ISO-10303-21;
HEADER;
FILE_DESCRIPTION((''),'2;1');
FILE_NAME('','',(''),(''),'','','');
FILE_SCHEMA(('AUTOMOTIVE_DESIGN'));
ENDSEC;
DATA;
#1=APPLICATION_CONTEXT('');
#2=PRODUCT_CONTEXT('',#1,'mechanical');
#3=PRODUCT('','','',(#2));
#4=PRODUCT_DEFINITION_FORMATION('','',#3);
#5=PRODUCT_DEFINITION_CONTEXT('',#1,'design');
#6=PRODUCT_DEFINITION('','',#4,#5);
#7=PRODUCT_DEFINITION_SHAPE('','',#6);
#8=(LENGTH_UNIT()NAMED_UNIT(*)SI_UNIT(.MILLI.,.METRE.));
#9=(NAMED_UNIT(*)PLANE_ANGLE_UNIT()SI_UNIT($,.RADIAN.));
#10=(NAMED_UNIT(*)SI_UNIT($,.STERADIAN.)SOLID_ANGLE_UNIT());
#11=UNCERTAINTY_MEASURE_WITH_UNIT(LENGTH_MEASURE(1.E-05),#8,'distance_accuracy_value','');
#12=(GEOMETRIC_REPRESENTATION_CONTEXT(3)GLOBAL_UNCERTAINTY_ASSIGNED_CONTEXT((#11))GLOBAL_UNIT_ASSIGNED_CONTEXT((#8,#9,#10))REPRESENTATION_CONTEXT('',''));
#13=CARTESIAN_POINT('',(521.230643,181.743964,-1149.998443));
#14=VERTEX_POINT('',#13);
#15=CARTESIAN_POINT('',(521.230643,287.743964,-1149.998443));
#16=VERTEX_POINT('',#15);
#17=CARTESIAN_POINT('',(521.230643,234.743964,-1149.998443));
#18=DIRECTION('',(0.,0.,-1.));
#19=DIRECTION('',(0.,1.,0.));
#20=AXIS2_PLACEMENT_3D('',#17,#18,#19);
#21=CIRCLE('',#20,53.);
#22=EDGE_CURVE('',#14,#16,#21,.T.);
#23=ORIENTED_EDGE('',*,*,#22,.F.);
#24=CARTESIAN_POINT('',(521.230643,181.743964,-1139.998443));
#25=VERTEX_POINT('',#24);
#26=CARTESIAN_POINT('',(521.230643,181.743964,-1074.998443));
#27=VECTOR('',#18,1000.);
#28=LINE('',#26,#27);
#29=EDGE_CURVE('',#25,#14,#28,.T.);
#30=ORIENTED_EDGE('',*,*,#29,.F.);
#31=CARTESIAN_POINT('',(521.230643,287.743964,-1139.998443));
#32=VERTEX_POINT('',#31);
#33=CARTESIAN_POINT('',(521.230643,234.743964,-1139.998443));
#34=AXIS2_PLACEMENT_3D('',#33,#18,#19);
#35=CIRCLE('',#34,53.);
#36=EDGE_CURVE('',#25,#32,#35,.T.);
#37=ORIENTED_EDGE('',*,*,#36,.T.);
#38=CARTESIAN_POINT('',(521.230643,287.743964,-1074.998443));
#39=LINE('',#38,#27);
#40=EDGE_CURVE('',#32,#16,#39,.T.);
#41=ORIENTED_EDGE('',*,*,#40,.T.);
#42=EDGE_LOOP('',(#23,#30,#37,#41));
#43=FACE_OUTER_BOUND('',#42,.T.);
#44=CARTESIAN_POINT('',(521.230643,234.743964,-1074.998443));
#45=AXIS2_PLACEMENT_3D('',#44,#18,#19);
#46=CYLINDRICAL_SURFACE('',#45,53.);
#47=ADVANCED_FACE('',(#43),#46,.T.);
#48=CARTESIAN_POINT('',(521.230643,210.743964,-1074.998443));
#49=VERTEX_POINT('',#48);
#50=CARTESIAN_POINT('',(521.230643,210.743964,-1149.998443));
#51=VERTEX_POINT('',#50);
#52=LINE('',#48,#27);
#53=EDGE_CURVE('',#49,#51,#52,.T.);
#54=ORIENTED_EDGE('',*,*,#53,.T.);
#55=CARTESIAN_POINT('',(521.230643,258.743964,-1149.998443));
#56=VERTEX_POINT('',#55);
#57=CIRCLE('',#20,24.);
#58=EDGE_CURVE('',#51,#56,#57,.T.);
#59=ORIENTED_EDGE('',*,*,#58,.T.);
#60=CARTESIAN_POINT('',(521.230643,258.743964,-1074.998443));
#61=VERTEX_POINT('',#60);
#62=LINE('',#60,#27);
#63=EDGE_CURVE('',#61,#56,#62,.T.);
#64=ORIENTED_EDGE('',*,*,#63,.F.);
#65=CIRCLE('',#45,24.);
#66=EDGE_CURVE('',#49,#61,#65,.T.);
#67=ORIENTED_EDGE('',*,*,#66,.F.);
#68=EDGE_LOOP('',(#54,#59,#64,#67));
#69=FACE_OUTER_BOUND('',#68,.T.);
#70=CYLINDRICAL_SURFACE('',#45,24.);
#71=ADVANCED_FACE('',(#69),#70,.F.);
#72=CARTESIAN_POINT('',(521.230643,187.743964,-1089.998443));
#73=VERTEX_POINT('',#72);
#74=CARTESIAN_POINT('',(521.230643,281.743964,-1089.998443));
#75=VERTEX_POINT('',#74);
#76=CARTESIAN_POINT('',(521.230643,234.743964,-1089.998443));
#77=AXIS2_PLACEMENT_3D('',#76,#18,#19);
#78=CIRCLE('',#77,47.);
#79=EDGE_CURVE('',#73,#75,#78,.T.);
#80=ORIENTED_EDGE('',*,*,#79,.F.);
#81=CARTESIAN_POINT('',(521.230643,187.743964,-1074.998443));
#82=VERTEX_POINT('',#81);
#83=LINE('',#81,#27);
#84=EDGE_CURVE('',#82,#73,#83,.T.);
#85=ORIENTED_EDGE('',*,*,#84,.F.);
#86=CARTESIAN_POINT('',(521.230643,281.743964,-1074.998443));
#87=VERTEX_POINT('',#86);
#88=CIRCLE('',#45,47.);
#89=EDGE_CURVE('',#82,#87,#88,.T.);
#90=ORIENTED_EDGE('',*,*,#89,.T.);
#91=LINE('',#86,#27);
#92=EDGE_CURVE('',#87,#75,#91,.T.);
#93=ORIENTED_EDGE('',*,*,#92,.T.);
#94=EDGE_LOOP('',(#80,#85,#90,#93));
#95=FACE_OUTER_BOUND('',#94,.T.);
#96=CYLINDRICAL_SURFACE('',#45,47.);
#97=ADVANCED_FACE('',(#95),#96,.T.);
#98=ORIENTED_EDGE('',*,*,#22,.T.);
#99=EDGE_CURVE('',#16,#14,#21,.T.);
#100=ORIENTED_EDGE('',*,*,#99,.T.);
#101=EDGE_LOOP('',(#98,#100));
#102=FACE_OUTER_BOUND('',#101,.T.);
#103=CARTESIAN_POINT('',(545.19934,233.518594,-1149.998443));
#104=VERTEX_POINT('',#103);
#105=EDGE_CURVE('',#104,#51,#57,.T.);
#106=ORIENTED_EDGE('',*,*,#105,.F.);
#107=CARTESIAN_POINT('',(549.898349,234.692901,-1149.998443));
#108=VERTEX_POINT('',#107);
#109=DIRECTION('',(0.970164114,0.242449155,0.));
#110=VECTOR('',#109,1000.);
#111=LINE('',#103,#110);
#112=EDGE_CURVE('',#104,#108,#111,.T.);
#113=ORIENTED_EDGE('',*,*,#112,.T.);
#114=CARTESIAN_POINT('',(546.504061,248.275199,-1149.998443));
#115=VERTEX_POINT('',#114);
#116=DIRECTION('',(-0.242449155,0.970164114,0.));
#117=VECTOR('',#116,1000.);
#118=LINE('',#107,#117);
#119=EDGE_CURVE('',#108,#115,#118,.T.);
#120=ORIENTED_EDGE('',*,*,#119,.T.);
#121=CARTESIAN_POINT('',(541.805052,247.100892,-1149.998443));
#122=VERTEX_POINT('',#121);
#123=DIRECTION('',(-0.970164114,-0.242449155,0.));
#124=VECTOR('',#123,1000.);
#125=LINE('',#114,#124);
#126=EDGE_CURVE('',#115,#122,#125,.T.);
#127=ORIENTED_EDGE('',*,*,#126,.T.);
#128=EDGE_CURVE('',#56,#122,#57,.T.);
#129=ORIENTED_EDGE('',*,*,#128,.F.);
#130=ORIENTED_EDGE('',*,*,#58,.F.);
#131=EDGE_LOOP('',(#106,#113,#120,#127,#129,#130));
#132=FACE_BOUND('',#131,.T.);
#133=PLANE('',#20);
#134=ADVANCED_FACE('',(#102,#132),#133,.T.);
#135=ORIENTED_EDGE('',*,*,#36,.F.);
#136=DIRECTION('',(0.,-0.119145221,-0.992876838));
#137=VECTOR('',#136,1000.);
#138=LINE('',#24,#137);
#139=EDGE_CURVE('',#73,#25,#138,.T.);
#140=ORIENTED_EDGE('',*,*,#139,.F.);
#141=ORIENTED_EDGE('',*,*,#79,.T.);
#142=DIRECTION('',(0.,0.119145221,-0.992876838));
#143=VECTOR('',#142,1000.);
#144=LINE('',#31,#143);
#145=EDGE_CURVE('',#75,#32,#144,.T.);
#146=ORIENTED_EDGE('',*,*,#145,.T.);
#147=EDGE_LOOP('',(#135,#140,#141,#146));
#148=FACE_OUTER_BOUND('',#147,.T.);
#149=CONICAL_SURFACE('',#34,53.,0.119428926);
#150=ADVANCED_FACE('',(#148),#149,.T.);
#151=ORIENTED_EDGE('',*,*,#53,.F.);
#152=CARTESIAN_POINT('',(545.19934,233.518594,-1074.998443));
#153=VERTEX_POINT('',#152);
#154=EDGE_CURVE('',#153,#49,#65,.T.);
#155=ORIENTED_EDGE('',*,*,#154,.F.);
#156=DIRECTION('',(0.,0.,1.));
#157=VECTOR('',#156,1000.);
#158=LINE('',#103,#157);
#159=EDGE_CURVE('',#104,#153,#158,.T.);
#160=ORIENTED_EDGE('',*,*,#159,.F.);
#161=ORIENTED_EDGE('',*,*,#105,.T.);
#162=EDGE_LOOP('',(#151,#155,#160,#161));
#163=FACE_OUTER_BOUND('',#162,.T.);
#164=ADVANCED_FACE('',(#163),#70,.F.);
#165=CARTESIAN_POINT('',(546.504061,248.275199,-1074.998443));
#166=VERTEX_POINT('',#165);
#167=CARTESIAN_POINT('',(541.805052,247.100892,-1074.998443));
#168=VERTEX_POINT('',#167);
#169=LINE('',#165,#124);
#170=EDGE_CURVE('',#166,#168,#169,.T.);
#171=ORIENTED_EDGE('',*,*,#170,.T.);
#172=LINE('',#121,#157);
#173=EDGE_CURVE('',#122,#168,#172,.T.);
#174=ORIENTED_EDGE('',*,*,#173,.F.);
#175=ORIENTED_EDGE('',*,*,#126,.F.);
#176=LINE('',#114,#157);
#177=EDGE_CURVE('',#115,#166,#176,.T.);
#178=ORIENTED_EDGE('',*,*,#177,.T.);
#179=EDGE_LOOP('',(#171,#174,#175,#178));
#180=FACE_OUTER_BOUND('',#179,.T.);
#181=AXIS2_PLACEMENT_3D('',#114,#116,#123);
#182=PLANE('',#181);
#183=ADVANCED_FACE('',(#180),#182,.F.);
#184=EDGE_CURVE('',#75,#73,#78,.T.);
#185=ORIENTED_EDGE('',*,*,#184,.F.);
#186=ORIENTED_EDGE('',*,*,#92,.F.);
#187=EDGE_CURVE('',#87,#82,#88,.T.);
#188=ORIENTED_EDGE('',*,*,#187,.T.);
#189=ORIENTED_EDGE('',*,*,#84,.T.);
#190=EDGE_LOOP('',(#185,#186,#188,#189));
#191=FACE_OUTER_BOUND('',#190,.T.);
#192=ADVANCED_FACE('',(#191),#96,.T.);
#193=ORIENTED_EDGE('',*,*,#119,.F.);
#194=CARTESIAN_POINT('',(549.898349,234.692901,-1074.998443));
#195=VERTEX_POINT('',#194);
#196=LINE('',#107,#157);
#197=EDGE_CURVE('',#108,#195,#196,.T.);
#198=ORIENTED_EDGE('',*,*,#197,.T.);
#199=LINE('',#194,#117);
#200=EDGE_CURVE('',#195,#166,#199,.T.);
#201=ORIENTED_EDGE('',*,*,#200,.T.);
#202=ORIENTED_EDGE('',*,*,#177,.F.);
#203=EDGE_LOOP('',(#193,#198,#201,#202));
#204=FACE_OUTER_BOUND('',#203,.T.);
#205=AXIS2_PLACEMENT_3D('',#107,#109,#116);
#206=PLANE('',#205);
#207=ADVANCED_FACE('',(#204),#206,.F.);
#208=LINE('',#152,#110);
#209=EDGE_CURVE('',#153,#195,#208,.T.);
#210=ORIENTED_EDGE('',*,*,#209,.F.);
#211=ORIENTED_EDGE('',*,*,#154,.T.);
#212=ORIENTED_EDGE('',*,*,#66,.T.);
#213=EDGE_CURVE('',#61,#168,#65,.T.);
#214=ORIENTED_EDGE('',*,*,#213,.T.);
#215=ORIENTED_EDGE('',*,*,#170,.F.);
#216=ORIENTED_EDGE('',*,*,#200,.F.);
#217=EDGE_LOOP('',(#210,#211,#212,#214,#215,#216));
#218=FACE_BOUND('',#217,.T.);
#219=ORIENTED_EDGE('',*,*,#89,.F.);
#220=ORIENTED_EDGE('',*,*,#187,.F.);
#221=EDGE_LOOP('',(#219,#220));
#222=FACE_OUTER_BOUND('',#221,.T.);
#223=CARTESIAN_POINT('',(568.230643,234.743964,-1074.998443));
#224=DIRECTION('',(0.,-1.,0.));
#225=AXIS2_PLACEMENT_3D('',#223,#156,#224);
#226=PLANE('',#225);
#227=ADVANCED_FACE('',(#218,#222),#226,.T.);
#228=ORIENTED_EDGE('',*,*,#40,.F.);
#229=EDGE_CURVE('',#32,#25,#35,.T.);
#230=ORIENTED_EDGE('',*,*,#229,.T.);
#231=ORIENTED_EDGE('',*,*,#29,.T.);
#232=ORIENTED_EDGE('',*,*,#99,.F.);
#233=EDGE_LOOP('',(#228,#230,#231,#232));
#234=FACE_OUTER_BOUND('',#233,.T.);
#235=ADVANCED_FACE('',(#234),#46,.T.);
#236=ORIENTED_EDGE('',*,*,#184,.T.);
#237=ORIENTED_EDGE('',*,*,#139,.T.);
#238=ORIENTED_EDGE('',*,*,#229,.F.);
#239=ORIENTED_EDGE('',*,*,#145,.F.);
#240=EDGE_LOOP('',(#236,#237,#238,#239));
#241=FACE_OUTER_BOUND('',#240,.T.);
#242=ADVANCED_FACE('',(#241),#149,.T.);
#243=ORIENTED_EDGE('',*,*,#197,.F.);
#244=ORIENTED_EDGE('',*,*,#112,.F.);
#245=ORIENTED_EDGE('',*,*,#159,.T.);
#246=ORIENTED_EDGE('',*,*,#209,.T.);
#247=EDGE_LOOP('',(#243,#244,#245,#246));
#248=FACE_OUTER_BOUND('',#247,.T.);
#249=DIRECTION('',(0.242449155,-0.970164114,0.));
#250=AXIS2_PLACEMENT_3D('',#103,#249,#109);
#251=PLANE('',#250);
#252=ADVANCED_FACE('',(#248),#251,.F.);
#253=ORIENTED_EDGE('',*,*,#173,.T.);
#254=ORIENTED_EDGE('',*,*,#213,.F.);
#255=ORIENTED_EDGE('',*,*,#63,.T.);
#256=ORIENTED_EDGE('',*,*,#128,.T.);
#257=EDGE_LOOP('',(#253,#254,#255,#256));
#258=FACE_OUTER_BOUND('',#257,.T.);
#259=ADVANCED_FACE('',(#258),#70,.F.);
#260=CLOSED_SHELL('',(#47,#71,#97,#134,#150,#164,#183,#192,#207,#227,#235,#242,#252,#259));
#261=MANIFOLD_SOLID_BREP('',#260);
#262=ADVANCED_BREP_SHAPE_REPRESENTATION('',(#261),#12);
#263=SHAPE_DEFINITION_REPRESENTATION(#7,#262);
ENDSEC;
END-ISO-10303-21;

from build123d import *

# Parameters (mm, degrees)
CUT_EXTRUDE1_DEPTH = 647.654791602
SKETCH3_W          = 24
SKETCH3_H          = 75


with BuildPart() as part:
    # Sketch1 → Revolve1 (revolve)
    with BuildSketch(Plane.XZ.offset(-234.743963655), mode=Mode.PRIVATE) as revolve1_sk:
        Polygon((568.230642584, -1074.998443067), (521.230642584, -1074.998443067), (521.230642584, -1149.998443067), (574.230642584, -1149.998443067), (574.230642584, -1139.998443067), (568.230642584, -1089.998443067), align=None)
    revolve(revolve1_sk.sketch.rotate(Axis((521.230642584, 234.743963655, -1074.998443067), (0, 0, -1)), 270), axis=Axis((521.230642584, 234.743963655, -1074.998443067), (0, 0, -1)))

    # Sketch2 → Cut-Extrude1 (cut, through all)
    with BuildSketch(Plane.XY.offset(-1074.998443067)):
        with BuildLine():
            Line((549.898349026, 234.692901362), (546.50406086, 248.275198952))
            Line((546.50406086, 248.275198952), (541.805052122, 247.10089176))
            ThreePointArc((541.805052122, 247.10089176), (544.514581311, 240.562743369), (545.199340288, 233.518594169))
            Line((545.199340288, 233.518594169), (549.898349026, 234.692901362))
        make_face()
    extrude(amount=-CUT_EXTRUDE1_DEPTH, mode=Mode.SUBTRACT)

    # Sketch3 → Cut-Revolve1 (revolve, cut)
    with BuildSketch(Plane.XZ.offset(-234.743963655)):
        with Locations((533.230642584, -1112.498443067)):
            Rectangle(SKETCH3_W, SKETCH3_H)
    revolve(axis=Axis((521.230642584, 234.743963655, -1074.998443067), (0, 0, -1)), mode=Mode.SUBTRACT)


solid = part.part
